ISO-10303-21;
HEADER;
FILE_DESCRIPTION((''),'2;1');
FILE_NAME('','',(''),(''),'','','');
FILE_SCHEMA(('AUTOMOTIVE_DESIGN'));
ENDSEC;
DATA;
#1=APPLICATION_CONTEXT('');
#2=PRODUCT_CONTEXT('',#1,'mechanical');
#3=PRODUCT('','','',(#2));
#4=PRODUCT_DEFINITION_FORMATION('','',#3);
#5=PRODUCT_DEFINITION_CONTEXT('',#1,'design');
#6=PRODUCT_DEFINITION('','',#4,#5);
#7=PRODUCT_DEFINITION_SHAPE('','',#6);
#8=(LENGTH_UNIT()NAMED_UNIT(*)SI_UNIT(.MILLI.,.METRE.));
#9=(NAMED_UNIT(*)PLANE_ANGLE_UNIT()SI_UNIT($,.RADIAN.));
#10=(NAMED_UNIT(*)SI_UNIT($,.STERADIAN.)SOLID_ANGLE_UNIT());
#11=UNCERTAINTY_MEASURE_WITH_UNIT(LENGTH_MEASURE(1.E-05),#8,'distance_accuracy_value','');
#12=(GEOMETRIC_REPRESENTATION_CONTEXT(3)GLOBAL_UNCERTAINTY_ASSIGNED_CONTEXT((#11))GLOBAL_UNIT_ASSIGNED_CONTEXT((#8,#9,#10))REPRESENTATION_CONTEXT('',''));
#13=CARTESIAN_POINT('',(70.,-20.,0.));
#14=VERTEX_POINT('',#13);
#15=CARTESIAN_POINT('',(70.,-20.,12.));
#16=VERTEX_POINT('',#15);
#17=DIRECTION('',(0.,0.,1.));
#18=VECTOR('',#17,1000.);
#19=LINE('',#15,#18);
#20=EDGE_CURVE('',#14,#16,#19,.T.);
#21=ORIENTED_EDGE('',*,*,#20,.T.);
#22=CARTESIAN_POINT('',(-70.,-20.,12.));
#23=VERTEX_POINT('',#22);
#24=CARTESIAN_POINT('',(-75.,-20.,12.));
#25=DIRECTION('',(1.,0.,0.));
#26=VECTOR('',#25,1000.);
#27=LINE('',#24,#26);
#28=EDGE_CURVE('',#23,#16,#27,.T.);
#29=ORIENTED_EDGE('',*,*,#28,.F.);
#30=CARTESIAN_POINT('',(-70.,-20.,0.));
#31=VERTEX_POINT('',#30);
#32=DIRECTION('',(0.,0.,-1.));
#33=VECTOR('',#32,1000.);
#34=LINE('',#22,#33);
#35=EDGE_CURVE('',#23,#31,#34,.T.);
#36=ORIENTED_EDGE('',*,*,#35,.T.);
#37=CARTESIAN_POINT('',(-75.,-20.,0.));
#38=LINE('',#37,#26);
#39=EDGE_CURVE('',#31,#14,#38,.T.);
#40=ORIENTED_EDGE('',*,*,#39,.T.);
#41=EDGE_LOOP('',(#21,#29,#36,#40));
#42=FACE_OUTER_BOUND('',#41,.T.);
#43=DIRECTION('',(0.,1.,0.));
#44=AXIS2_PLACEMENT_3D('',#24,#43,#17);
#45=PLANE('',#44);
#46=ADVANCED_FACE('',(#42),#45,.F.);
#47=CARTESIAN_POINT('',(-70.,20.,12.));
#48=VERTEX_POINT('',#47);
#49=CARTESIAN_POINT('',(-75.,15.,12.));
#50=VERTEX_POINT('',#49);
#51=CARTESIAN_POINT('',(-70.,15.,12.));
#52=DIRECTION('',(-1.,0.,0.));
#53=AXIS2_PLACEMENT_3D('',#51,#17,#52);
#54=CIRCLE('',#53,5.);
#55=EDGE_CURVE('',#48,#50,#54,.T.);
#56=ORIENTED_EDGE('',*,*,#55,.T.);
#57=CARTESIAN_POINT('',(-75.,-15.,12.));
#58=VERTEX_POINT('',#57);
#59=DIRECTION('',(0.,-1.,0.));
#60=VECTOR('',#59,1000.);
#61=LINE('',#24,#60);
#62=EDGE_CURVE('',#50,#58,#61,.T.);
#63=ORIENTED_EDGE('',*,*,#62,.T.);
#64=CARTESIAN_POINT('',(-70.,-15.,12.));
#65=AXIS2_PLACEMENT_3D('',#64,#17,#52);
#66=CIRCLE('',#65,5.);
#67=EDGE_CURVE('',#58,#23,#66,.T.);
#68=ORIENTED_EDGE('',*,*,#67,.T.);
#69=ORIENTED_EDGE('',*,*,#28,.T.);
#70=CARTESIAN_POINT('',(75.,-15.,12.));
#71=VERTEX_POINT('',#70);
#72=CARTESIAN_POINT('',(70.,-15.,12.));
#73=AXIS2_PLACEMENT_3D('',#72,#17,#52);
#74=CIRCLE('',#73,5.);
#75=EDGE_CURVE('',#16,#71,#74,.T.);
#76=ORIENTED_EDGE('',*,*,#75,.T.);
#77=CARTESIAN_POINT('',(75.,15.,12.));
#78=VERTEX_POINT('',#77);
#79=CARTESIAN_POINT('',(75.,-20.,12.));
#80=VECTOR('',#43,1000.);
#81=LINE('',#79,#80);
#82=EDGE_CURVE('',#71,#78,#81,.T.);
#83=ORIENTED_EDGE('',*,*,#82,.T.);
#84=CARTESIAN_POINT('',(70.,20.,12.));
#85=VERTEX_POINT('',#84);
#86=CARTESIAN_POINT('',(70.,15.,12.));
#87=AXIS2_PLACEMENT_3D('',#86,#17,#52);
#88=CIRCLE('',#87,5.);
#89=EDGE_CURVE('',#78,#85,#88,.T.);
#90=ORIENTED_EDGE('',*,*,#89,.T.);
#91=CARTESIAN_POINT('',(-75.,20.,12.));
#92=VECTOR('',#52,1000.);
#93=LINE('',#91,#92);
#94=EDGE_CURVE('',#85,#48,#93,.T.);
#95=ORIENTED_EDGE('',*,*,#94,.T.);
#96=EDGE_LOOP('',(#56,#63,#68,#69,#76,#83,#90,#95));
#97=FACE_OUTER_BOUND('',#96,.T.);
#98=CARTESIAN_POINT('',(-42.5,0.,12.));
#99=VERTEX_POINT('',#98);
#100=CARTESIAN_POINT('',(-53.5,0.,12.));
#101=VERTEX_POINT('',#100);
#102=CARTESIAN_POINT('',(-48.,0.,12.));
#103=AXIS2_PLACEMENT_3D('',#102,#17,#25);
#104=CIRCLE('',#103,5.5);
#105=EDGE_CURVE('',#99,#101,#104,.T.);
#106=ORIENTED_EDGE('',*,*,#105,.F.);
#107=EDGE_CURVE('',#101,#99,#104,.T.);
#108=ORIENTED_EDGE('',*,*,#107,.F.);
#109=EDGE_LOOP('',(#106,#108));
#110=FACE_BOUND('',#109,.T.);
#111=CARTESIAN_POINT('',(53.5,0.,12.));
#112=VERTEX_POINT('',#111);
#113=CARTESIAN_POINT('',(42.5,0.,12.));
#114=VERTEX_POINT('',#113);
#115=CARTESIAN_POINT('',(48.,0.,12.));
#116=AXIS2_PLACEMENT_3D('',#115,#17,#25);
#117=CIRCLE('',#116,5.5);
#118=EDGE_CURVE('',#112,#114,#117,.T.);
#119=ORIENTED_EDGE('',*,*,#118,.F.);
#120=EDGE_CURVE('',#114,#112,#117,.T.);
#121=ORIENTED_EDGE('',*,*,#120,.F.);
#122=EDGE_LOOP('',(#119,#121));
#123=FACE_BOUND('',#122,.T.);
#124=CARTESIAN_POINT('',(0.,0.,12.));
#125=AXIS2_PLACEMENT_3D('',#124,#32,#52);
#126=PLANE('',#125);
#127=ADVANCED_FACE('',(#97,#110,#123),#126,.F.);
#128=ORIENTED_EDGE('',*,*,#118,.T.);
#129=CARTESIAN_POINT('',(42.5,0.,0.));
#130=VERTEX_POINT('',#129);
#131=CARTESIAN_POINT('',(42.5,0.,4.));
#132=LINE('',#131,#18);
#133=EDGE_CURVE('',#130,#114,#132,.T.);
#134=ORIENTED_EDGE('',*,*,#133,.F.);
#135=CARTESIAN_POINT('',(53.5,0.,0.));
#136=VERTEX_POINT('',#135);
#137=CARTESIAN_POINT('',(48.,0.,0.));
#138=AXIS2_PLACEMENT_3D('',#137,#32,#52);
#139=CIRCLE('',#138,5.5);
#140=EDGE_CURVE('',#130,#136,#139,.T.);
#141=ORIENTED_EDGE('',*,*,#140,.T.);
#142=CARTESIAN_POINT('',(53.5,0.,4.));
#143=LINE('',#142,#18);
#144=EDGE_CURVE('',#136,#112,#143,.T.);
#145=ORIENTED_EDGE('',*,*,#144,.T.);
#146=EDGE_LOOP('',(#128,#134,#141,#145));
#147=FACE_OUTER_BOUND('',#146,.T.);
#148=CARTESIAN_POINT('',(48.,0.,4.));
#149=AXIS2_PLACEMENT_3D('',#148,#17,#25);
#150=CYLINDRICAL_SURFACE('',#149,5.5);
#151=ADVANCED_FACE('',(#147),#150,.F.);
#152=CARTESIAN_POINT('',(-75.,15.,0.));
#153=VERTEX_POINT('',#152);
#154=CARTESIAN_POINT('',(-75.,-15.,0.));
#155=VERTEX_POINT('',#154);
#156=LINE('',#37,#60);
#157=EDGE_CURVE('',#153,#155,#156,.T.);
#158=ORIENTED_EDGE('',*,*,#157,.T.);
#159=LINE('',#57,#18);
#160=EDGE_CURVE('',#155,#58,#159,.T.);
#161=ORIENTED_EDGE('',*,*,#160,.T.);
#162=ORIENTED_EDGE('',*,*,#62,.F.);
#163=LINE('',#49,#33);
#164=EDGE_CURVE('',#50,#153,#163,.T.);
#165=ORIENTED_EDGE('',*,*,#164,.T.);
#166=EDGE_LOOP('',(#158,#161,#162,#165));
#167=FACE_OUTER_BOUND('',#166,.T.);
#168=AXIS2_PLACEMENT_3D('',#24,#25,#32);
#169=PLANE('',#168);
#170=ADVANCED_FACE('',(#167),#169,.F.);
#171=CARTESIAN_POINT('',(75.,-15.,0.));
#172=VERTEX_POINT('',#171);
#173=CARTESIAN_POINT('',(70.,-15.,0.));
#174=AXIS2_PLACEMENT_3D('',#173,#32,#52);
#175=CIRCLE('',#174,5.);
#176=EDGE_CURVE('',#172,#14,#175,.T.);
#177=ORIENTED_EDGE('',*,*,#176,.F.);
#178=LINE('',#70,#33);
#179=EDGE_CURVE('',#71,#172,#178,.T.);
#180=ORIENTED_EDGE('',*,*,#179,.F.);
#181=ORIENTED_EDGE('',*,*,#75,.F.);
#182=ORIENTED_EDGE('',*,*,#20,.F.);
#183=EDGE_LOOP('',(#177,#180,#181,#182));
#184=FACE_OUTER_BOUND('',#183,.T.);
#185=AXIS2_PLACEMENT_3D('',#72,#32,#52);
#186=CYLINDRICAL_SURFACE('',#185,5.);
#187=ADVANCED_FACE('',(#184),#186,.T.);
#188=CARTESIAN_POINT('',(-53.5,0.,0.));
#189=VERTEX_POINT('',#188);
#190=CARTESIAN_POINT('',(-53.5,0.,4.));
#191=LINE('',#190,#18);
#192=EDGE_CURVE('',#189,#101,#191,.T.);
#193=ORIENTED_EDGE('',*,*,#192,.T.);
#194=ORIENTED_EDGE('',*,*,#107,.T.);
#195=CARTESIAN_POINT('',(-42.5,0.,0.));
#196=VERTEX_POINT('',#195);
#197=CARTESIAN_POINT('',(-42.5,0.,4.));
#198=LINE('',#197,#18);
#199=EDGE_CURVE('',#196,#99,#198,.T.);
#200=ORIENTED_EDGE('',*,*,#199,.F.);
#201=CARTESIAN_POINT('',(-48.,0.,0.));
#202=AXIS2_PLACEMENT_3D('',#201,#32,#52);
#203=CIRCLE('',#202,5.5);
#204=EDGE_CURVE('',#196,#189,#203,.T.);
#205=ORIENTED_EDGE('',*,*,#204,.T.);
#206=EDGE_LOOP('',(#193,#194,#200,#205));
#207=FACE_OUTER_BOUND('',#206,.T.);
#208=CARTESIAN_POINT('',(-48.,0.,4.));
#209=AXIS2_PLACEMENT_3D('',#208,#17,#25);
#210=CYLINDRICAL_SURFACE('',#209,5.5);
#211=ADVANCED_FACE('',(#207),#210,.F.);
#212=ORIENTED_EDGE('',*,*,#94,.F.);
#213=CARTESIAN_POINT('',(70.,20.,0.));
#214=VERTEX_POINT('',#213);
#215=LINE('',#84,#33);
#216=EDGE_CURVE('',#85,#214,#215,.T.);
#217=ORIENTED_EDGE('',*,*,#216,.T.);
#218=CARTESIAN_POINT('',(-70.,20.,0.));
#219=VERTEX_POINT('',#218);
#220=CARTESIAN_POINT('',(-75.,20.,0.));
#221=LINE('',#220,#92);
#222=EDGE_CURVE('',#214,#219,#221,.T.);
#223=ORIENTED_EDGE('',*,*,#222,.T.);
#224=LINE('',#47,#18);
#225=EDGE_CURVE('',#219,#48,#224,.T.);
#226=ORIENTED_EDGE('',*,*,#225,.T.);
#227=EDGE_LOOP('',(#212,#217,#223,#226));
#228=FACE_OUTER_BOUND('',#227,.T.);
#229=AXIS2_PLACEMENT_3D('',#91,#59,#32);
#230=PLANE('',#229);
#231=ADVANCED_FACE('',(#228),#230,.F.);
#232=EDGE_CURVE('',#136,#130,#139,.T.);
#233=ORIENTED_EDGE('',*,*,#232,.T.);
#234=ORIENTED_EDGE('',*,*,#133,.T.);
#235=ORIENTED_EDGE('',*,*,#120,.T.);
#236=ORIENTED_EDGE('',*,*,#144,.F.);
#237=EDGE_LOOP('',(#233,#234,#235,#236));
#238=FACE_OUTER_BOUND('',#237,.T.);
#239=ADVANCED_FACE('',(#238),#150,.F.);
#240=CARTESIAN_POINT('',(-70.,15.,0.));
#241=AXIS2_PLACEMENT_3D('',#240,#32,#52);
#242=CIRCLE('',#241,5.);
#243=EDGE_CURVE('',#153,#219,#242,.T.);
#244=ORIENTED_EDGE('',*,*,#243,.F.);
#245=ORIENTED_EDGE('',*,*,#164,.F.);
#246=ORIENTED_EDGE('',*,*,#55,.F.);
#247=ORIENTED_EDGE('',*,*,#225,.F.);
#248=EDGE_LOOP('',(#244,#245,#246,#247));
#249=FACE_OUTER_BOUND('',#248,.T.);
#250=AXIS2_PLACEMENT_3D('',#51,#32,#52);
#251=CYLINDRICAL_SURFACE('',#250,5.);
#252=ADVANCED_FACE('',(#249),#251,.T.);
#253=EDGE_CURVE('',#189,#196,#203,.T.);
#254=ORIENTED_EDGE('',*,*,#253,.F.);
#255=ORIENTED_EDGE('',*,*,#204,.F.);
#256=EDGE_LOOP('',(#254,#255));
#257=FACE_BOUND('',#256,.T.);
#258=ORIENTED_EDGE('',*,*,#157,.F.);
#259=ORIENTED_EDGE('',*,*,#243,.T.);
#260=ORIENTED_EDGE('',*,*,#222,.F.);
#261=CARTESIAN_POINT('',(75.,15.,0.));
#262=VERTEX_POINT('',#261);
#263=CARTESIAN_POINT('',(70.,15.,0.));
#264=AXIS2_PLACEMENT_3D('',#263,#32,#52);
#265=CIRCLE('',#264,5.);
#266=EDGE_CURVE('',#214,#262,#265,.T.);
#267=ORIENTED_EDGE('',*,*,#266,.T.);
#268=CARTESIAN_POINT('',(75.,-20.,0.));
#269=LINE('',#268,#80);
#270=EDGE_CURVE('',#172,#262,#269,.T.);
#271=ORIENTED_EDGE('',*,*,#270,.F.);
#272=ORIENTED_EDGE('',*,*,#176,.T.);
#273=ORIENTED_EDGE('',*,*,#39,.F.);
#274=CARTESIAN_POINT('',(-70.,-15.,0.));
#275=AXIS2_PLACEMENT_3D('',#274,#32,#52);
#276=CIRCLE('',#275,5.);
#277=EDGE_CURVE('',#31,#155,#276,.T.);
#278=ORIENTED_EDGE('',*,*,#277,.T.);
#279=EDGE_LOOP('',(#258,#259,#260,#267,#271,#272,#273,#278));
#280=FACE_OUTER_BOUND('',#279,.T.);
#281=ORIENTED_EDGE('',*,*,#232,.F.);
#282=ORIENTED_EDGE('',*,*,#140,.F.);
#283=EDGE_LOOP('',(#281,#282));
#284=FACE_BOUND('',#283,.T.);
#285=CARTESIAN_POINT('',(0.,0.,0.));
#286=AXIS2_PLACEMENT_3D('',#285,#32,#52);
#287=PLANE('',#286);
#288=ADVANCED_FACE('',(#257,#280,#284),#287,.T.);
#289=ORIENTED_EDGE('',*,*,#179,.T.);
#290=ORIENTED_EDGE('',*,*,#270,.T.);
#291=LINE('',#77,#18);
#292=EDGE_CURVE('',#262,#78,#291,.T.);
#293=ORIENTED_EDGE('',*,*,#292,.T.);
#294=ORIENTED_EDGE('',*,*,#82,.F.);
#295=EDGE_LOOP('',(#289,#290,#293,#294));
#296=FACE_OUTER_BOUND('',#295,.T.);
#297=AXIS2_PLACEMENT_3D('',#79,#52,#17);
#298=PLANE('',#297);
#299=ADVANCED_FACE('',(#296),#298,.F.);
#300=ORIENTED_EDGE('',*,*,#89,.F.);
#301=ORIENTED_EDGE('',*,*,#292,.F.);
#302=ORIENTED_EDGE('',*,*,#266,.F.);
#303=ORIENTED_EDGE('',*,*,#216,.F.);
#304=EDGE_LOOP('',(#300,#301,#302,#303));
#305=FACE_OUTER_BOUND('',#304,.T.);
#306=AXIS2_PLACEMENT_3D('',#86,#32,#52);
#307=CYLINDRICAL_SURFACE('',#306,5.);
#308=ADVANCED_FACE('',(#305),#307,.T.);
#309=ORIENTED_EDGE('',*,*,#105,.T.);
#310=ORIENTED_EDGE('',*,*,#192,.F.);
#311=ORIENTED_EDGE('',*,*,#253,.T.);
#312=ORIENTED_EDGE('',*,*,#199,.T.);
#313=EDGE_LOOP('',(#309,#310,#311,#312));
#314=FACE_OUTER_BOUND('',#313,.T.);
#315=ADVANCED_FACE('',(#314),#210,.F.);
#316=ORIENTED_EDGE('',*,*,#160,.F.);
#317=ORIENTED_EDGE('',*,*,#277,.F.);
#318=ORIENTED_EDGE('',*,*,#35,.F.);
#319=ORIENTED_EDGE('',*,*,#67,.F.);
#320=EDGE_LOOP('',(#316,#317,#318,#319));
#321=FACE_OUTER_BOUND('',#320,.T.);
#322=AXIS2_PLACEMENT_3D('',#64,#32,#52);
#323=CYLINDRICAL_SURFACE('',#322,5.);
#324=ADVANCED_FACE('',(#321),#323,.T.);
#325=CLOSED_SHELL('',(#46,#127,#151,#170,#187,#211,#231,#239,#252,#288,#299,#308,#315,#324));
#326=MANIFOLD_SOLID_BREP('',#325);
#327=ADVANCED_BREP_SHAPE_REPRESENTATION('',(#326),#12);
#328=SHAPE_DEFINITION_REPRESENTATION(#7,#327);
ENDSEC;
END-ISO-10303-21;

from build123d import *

# Parameters (mm, degrees)
SKETCH1_W           = 150
SKETCH1_H           = 40
BOSS_EXTRUDE1_DEPTH = 12
SKETCH2_R           = 5.5
CUT_EXTRUDE1_DEPTH  = 8
FILLET1_R           = 5
CUT_EXTRUDE2_START  = -12
SKETCH3_R           = 5.5
CUT_EXTRUDE2_DEPTH  = 12


with BuildPart() as part:
    # Sketch1 → Boss-Extrude1 (new body)
    with BuildSketch(Plane.XY):
        Rectangle(SKETCH1_W, SKETCH1_H)
    extrude(amount=BOSS_EXTRUDE1_DEPTH)

    # Sketch2 → Cut-Extrude1 (cut)
    with BuildSketch(Plane.XY.offset(12)):
        with Locations((-48, 0)):
            Circle(SKETCH2_R)
        with Locations((48, 0)):
            Circle(SKETCH2_R)
    extrude(amount=-CUT_EXTRUDE1_DEPTH, mode=Mode.SUBTRACT)

    # Fillet1
    fillet1_edges = [part.edges().sort_by_distance(p)[0] for p in [
        (75, -20, 6),
        (-75, -20, 6),
        (-75, 20, 6),
        (75, 20, 6),
    ]]
    fillet(fillet1_edges, radius=FILLET1_R)

    # Sketch3 → Cut-Extrude2 (cut)
    with BuildSketch(Plane(origin=(0, 0, 0), x_dir=(-1, 0, 0), z_dir=(0, 0, -1)).offset(CUT_EXTRUDE2_START)):
        with Locations(Location((-48, 0, 0), (0, 0, 180))):
            Circle(SKETCH3_R)
        with Locations(Location((48, 0, 0), (0, 0, 180))):
            Circle(SKETCH3_R)
    extrude(amount=CUT_EXTRUDE2_DEPTH, mode=Mode.SUBTRACT)


solid = part.part
